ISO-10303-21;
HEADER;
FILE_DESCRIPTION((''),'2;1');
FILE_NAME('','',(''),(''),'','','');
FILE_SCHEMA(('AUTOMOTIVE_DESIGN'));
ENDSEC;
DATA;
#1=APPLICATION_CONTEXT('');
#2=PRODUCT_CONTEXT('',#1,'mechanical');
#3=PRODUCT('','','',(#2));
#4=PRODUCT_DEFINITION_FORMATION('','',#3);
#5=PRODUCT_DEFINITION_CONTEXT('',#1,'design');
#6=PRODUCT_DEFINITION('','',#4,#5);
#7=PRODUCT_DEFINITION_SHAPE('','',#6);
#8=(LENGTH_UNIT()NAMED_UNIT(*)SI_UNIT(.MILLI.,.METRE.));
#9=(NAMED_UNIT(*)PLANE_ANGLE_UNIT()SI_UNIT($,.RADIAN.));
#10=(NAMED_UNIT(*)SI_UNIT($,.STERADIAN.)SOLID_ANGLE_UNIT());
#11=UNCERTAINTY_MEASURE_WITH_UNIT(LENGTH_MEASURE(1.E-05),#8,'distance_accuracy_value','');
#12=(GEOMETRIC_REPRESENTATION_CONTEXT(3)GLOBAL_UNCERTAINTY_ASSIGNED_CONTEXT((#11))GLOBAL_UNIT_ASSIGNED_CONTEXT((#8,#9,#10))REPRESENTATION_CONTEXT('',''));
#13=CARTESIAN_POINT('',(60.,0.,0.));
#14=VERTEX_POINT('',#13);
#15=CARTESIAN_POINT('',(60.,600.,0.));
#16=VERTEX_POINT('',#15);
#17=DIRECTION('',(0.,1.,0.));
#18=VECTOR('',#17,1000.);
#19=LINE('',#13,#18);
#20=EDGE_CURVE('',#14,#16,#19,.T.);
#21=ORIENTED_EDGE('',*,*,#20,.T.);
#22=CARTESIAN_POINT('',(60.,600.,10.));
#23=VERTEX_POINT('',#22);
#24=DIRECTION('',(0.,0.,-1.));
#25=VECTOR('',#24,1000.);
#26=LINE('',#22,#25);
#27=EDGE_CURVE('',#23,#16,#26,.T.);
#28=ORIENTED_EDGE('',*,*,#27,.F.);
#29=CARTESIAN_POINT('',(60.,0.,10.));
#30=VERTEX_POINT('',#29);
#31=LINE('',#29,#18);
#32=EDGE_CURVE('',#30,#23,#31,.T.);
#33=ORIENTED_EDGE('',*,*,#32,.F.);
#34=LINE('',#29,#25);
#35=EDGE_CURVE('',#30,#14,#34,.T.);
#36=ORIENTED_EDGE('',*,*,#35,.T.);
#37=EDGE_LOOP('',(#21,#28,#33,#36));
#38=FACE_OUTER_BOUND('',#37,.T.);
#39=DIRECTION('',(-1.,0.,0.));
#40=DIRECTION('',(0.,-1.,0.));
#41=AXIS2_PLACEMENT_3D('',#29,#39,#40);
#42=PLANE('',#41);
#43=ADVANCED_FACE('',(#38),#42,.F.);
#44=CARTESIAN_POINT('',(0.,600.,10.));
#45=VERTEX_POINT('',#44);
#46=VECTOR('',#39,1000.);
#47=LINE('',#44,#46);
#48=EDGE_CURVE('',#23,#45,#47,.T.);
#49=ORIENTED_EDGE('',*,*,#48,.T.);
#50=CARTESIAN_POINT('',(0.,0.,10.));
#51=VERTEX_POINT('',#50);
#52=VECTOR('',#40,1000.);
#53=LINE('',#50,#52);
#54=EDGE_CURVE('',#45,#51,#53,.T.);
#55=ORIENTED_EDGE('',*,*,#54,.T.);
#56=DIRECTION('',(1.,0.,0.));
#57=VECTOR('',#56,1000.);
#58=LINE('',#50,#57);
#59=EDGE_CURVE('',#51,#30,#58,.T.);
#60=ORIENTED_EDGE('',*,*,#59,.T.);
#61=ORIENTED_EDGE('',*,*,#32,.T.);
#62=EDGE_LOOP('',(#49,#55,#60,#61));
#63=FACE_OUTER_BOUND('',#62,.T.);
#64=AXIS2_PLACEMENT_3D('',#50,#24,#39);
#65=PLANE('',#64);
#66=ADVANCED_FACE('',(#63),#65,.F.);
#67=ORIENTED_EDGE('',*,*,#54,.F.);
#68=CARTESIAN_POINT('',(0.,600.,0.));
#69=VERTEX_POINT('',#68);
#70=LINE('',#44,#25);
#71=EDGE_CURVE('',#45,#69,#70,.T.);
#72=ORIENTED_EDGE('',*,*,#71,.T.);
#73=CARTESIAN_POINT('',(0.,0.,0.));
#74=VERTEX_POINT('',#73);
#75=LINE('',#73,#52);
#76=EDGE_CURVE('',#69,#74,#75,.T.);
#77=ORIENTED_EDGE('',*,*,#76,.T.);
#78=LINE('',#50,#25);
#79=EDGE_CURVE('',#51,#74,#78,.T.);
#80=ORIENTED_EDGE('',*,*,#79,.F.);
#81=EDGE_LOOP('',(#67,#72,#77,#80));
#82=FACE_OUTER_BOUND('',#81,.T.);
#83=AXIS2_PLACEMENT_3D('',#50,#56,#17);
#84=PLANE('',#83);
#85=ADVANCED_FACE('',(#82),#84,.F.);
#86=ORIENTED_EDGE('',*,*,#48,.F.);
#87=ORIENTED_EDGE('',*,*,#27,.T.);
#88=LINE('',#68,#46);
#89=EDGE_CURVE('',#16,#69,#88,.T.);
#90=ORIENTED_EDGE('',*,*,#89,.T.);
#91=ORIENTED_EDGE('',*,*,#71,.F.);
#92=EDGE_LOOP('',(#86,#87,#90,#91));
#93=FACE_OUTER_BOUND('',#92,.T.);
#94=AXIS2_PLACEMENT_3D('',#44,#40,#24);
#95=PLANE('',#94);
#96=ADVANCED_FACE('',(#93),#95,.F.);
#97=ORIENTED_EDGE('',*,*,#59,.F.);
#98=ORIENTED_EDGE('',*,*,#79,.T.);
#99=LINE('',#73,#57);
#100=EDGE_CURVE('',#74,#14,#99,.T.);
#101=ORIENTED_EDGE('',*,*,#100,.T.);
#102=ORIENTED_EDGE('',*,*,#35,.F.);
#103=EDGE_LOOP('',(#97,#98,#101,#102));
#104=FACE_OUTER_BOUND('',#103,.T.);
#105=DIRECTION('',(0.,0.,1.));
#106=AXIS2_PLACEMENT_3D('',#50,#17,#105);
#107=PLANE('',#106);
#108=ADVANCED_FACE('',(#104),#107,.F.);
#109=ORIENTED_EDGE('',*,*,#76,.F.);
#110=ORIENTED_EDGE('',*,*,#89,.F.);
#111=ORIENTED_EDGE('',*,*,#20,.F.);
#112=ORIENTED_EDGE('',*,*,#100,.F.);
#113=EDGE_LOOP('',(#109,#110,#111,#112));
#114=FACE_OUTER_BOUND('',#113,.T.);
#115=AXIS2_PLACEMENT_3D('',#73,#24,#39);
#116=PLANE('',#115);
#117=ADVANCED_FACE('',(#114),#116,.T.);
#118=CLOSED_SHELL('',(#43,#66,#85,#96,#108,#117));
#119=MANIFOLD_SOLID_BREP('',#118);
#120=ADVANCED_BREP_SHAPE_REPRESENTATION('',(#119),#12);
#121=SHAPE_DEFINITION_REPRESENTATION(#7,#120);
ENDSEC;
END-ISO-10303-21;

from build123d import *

# Parameters (mm, degrees)
SKETCH1_W           = 60
SKETCH1_H           = 600
BOSS_EXTRUDE1_DEPTH = 10


with BuildPart() as part:
    # Sketch1 → Boss-Extrude1 (new body)
    with BuildSketch(Plane.XY):
        with Locations((30, 300)):
            Rectangle(SKETCH1_W, SKETCH1_H)
    extrude(amount=BOSS_EXTRUDE1_DEPTH)


solid = part.part
